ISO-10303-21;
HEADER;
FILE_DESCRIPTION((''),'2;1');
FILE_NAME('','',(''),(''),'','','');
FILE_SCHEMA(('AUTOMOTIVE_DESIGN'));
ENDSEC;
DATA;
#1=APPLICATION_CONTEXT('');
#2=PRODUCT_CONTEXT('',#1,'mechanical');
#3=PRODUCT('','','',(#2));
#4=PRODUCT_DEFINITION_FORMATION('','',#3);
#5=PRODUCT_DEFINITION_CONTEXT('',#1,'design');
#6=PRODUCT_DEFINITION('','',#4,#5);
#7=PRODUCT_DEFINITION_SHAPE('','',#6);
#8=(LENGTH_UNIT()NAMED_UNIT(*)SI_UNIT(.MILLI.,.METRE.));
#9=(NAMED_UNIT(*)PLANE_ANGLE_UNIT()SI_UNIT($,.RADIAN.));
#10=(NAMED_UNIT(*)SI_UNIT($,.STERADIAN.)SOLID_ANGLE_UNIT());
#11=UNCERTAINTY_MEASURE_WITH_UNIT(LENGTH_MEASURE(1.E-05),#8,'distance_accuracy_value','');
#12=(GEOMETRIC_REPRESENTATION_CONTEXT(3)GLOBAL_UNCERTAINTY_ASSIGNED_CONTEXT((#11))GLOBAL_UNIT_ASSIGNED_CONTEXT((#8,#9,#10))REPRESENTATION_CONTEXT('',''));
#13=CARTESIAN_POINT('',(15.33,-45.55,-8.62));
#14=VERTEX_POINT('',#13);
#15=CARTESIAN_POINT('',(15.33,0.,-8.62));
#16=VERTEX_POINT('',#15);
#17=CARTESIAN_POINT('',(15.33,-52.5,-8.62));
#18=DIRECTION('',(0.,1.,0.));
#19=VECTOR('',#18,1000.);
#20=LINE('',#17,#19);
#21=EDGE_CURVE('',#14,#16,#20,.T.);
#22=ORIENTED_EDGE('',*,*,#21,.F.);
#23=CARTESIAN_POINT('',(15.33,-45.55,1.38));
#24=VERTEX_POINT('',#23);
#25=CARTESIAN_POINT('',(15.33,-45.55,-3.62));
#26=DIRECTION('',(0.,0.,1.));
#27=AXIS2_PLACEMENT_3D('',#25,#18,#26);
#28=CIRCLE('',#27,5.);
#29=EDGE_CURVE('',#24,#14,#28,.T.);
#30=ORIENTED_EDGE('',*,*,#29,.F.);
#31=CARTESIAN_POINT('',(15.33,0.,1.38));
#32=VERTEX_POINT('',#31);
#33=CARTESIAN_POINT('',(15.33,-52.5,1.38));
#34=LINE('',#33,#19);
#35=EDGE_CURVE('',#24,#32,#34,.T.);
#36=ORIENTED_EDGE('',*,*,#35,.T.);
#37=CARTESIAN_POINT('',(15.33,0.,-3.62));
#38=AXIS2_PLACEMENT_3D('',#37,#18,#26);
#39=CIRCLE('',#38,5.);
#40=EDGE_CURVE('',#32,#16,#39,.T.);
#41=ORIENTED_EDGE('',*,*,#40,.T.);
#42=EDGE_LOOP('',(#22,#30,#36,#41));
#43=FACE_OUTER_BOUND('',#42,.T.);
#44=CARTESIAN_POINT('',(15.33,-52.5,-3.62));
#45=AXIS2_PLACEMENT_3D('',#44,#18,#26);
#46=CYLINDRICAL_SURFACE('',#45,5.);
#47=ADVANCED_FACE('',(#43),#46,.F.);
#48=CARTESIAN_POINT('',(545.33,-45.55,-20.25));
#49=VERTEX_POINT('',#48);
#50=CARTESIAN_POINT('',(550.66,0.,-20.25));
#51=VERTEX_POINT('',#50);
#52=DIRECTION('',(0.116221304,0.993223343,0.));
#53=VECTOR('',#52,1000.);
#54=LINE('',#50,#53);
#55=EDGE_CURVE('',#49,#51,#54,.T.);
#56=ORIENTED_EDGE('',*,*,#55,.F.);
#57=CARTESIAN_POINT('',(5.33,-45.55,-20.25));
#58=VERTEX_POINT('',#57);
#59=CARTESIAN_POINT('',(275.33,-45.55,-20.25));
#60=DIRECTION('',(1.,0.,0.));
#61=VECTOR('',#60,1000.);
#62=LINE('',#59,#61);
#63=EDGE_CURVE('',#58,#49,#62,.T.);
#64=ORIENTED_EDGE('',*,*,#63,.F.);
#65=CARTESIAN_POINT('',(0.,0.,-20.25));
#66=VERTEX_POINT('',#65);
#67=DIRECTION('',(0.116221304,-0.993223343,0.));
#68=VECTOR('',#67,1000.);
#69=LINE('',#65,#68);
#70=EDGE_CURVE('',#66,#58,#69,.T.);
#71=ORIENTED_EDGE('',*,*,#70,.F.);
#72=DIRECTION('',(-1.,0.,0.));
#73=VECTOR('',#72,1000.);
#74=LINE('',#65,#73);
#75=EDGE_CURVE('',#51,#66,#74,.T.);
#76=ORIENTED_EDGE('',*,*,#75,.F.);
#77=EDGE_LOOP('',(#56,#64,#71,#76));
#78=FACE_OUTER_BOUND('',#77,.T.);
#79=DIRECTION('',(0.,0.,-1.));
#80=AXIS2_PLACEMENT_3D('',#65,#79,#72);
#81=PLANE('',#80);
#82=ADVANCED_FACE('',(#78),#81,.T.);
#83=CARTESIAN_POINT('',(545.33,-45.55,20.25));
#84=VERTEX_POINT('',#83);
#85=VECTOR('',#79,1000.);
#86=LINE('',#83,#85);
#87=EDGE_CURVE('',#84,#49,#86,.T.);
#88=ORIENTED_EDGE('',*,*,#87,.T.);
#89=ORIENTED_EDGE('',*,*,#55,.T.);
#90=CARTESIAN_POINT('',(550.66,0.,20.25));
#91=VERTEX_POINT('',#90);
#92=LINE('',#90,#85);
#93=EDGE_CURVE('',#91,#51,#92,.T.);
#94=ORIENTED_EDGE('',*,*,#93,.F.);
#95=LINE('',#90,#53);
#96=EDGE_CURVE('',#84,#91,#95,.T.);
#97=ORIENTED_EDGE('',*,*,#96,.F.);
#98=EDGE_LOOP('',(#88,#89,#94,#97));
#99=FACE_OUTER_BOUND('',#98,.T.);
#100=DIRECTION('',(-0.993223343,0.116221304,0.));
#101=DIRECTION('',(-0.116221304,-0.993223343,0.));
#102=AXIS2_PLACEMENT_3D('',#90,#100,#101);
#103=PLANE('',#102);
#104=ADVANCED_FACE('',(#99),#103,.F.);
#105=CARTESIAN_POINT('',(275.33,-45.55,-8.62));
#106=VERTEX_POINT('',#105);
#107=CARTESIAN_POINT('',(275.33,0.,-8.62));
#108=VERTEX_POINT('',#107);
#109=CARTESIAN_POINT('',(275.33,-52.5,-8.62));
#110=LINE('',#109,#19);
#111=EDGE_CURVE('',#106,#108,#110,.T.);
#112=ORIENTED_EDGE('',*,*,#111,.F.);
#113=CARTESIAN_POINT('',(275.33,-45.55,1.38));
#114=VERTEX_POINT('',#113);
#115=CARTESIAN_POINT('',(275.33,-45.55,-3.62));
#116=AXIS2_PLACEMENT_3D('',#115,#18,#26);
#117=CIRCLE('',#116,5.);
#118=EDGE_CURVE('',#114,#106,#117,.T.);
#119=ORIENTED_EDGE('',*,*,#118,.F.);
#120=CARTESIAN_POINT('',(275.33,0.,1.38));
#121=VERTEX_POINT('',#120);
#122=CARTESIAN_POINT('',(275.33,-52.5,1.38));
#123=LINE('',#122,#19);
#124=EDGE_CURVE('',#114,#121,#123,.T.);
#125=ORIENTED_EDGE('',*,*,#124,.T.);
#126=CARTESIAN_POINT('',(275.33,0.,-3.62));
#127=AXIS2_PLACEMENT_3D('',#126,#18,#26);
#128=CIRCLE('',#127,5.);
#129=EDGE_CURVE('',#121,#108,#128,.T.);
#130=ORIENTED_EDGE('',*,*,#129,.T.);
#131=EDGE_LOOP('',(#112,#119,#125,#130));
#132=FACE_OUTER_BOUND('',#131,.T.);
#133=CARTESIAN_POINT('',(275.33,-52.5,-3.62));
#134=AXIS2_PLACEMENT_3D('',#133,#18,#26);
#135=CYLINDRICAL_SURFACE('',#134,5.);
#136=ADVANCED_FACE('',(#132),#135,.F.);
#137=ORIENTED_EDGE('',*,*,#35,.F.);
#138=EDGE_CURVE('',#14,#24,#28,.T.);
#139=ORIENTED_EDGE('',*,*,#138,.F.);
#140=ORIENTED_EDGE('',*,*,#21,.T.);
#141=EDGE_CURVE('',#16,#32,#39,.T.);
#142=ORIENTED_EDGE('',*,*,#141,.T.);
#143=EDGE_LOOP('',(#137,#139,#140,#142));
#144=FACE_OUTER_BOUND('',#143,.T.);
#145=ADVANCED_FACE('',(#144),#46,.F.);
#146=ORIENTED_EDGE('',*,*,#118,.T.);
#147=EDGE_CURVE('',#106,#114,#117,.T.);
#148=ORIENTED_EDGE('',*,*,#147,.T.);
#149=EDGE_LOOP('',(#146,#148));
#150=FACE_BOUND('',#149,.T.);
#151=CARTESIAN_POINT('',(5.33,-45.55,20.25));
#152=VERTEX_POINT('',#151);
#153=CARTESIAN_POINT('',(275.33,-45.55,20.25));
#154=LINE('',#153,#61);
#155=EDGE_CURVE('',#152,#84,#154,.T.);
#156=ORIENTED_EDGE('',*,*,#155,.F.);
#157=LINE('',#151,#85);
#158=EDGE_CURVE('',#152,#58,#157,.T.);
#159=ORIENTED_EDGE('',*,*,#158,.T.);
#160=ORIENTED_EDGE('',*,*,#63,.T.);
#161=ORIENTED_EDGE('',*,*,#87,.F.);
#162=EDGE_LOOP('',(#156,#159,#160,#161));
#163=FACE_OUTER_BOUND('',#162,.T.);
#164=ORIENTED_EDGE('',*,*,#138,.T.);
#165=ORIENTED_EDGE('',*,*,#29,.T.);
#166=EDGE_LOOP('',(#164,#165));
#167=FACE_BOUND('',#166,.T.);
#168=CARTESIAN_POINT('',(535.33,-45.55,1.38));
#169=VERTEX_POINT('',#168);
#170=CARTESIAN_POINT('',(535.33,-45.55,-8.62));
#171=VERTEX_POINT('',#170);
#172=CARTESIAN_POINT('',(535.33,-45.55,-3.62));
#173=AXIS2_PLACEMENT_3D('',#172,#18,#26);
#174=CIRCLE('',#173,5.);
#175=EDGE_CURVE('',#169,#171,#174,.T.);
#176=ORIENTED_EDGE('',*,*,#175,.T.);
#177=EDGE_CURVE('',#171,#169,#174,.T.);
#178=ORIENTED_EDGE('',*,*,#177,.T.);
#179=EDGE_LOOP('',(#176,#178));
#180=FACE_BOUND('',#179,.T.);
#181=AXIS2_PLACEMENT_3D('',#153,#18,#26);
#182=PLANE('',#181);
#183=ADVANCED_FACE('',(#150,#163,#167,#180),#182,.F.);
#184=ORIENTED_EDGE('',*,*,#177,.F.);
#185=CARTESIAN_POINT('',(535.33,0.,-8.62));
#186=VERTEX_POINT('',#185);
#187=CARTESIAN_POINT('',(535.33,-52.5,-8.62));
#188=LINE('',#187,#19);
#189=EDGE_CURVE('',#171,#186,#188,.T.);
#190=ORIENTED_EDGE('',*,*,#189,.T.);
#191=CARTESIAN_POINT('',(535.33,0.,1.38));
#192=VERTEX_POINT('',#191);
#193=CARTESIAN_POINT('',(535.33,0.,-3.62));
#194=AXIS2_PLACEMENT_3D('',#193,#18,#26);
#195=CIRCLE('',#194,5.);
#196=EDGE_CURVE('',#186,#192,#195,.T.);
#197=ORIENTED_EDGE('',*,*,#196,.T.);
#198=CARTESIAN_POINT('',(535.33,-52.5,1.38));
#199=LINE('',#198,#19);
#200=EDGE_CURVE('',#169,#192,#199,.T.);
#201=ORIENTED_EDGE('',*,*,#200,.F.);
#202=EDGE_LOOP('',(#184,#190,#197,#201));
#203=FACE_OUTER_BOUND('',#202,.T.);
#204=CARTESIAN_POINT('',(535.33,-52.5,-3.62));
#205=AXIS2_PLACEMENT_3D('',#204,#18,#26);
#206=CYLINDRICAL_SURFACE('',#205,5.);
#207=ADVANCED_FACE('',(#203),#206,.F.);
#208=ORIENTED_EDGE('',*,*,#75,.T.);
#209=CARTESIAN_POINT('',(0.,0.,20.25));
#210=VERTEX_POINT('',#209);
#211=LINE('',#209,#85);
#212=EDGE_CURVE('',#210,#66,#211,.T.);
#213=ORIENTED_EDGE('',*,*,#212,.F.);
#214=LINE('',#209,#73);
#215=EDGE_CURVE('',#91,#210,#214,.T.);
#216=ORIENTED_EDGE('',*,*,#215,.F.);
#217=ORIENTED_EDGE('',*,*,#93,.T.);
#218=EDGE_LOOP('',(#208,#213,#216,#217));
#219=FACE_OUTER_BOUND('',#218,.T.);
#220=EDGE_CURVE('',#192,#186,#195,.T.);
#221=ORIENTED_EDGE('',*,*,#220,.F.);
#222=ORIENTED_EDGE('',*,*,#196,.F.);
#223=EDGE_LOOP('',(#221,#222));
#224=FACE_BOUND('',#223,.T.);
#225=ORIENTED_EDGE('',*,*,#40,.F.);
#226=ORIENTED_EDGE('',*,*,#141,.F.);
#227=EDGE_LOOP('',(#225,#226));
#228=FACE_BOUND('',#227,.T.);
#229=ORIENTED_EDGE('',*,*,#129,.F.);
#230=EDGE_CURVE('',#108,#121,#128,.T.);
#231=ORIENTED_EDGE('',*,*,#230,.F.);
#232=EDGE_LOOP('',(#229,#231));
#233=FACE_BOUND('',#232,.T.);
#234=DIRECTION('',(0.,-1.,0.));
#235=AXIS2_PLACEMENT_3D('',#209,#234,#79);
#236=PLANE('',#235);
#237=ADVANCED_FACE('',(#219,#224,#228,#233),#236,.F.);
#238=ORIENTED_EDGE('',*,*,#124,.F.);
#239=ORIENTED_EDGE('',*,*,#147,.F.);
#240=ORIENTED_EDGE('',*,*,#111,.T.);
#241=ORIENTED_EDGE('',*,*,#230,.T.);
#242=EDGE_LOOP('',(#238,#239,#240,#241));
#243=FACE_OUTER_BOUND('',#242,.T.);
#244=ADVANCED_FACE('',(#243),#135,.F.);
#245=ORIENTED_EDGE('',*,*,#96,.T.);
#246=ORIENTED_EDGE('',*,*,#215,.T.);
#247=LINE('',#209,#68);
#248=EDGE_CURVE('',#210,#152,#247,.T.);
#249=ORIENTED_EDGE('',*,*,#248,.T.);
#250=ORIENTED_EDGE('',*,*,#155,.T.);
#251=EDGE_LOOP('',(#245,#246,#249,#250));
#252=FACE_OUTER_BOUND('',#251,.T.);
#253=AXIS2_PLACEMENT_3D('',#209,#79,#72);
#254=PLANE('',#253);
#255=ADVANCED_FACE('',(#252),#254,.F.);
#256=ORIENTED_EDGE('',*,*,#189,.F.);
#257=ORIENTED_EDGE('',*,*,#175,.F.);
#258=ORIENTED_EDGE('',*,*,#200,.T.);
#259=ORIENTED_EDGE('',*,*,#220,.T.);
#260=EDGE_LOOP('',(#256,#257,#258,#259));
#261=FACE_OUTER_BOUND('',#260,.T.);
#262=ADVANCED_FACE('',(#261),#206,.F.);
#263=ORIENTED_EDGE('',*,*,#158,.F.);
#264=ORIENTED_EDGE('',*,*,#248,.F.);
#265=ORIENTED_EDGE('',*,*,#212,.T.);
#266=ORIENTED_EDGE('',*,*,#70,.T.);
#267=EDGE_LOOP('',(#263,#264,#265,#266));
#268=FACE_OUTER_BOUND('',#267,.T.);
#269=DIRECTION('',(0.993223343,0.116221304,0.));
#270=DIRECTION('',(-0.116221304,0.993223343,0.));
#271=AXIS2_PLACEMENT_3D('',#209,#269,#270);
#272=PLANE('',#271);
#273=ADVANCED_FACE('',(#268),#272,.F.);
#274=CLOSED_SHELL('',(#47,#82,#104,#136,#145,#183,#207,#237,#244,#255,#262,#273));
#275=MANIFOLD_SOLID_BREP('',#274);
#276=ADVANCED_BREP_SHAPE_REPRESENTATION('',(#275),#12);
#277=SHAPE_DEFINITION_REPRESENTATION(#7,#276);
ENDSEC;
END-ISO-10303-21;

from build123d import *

# Parameters (mm, degrees)
EXTRUDE_1_DEPTH     = 20.25
SKETCH_2_R          = 5
CUT_EXTRUDE_1_DEPTH = 52.5


with BuildPart() as part:
    # 草图1 → 凸台-拉伸1 (new, symmetric)
    with BuildSketch(Plane.XY):
        Polygon((0, 0), (550.66, 0), (545.33, -45.55), (275.33, -45.55), (5.33, -45.55), align=None)
    extrude(amount=EXTRUDE_1_DEPTH, both=True)

    # 草图2 → 切除-拉伸1 (cut)
    with BuildSketch(Plane(origin=(0, 0, 0), x_dir=(1, 0, 0), z_dir=(0, 1, 0))):
        with Locations(Location((535.33, 3.62, 0), (0, 0, 270))):
            Circle(SKETCH_2_R)
        with Locations(Location((275.33, 3.62, 0), (0, 0, 270))):
            Circle(SKETCH_2_R)
        with Locations(Location((15.33, 3.62, 0), (0, 0, 270))):
            Circle(SKETCH_2_R)
    extrude(amount=-CUT_EXTRUDE_1_DEPTH, mode=Mode.SUBTRACT)


solid = part.part
